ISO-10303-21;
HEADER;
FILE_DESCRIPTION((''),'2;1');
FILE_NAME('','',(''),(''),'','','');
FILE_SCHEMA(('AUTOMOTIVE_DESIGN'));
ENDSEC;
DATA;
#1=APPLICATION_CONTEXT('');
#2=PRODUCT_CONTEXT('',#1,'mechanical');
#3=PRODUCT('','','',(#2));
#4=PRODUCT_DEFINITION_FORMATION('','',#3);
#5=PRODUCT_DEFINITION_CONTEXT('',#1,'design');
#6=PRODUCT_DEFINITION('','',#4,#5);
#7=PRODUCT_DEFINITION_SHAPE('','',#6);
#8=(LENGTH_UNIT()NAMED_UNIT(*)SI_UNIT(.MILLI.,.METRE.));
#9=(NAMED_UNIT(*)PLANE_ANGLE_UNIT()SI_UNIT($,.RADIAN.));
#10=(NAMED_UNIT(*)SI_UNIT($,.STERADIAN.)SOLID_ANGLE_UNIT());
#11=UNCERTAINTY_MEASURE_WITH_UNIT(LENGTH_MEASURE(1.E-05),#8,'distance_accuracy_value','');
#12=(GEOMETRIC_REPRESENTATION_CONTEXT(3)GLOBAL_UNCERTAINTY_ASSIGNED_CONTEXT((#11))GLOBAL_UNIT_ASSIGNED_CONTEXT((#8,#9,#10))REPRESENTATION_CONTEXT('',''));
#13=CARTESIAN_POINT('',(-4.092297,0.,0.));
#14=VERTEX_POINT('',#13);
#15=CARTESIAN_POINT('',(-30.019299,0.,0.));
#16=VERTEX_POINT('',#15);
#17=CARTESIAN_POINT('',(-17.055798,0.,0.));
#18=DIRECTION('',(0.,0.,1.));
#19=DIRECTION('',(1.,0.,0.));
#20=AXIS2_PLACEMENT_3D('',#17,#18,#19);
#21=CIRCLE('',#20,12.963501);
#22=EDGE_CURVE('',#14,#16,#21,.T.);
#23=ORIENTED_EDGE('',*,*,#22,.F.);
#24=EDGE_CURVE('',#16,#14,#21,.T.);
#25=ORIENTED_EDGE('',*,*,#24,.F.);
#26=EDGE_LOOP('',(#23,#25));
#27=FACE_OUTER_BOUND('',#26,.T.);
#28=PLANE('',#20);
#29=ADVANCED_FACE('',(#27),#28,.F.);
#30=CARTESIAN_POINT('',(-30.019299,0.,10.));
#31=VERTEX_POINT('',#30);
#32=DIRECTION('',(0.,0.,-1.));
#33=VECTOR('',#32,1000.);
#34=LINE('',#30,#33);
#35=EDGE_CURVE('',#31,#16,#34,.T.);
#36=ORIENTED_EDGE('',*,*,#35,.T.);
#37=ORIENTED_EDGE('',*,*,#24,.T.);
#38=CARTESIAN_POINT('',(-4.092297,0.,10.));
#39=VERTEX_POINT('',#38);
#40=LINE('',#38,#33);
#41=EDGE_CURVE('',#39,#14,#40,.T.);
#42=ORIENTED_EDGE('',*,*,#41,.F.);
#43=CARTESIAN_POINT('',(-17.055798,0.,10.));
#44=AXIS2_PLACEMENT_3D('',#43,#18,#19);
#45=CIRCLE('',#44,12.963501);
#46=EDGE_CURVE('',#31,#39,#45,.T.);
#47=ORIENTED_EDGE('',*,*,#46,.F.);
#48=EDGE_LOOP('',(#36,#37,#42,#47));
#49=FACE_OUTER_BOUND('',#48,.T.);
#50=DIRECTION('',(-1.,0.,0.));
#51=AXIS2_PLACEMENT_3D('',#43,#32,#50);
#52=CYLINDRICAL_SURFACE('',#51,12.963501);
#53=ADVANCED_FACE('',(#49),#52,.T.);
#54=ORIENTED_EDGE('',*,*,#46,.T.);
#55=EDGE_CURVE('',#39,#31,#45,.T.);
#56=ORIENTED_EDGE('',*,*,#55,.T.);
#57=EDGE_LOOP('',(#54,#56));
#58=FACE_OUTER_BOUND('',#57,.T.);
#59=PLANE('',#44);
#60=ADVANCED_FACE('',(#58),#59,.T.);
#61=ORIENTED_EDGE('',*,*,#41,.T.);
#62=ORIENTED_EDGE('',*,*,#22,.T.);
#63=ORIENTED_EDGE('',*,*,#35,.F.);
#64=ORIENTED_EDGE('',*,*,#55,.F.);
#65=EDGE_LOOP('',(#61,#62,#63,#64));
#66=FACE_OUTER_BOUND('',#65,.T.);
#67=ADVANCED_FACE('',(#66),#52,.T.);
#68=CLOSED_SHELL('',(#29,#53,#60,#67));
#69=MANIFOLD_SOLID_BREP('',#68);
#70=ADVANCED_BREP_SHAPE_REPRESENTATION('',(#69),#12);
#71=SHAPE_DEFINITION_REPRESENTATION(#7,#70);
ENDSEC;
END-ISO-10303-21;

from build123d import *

# Parameters (mm, degrees)
SKETCH1_R           = 12.963501109
BOSS_EXTRUDE1_DEPTH = 10


with BuildPart() as part:
    # Sketch1 → Boss-Extrude1 (new body)
    with BuildSketch(Plane.XY):
        with Locations((-17.055797946, 0)):
            Circle(SKETCH1_R)
    extrude(amount=BOSS_EXTRUDE1_DEPTH)


solid = part.part
